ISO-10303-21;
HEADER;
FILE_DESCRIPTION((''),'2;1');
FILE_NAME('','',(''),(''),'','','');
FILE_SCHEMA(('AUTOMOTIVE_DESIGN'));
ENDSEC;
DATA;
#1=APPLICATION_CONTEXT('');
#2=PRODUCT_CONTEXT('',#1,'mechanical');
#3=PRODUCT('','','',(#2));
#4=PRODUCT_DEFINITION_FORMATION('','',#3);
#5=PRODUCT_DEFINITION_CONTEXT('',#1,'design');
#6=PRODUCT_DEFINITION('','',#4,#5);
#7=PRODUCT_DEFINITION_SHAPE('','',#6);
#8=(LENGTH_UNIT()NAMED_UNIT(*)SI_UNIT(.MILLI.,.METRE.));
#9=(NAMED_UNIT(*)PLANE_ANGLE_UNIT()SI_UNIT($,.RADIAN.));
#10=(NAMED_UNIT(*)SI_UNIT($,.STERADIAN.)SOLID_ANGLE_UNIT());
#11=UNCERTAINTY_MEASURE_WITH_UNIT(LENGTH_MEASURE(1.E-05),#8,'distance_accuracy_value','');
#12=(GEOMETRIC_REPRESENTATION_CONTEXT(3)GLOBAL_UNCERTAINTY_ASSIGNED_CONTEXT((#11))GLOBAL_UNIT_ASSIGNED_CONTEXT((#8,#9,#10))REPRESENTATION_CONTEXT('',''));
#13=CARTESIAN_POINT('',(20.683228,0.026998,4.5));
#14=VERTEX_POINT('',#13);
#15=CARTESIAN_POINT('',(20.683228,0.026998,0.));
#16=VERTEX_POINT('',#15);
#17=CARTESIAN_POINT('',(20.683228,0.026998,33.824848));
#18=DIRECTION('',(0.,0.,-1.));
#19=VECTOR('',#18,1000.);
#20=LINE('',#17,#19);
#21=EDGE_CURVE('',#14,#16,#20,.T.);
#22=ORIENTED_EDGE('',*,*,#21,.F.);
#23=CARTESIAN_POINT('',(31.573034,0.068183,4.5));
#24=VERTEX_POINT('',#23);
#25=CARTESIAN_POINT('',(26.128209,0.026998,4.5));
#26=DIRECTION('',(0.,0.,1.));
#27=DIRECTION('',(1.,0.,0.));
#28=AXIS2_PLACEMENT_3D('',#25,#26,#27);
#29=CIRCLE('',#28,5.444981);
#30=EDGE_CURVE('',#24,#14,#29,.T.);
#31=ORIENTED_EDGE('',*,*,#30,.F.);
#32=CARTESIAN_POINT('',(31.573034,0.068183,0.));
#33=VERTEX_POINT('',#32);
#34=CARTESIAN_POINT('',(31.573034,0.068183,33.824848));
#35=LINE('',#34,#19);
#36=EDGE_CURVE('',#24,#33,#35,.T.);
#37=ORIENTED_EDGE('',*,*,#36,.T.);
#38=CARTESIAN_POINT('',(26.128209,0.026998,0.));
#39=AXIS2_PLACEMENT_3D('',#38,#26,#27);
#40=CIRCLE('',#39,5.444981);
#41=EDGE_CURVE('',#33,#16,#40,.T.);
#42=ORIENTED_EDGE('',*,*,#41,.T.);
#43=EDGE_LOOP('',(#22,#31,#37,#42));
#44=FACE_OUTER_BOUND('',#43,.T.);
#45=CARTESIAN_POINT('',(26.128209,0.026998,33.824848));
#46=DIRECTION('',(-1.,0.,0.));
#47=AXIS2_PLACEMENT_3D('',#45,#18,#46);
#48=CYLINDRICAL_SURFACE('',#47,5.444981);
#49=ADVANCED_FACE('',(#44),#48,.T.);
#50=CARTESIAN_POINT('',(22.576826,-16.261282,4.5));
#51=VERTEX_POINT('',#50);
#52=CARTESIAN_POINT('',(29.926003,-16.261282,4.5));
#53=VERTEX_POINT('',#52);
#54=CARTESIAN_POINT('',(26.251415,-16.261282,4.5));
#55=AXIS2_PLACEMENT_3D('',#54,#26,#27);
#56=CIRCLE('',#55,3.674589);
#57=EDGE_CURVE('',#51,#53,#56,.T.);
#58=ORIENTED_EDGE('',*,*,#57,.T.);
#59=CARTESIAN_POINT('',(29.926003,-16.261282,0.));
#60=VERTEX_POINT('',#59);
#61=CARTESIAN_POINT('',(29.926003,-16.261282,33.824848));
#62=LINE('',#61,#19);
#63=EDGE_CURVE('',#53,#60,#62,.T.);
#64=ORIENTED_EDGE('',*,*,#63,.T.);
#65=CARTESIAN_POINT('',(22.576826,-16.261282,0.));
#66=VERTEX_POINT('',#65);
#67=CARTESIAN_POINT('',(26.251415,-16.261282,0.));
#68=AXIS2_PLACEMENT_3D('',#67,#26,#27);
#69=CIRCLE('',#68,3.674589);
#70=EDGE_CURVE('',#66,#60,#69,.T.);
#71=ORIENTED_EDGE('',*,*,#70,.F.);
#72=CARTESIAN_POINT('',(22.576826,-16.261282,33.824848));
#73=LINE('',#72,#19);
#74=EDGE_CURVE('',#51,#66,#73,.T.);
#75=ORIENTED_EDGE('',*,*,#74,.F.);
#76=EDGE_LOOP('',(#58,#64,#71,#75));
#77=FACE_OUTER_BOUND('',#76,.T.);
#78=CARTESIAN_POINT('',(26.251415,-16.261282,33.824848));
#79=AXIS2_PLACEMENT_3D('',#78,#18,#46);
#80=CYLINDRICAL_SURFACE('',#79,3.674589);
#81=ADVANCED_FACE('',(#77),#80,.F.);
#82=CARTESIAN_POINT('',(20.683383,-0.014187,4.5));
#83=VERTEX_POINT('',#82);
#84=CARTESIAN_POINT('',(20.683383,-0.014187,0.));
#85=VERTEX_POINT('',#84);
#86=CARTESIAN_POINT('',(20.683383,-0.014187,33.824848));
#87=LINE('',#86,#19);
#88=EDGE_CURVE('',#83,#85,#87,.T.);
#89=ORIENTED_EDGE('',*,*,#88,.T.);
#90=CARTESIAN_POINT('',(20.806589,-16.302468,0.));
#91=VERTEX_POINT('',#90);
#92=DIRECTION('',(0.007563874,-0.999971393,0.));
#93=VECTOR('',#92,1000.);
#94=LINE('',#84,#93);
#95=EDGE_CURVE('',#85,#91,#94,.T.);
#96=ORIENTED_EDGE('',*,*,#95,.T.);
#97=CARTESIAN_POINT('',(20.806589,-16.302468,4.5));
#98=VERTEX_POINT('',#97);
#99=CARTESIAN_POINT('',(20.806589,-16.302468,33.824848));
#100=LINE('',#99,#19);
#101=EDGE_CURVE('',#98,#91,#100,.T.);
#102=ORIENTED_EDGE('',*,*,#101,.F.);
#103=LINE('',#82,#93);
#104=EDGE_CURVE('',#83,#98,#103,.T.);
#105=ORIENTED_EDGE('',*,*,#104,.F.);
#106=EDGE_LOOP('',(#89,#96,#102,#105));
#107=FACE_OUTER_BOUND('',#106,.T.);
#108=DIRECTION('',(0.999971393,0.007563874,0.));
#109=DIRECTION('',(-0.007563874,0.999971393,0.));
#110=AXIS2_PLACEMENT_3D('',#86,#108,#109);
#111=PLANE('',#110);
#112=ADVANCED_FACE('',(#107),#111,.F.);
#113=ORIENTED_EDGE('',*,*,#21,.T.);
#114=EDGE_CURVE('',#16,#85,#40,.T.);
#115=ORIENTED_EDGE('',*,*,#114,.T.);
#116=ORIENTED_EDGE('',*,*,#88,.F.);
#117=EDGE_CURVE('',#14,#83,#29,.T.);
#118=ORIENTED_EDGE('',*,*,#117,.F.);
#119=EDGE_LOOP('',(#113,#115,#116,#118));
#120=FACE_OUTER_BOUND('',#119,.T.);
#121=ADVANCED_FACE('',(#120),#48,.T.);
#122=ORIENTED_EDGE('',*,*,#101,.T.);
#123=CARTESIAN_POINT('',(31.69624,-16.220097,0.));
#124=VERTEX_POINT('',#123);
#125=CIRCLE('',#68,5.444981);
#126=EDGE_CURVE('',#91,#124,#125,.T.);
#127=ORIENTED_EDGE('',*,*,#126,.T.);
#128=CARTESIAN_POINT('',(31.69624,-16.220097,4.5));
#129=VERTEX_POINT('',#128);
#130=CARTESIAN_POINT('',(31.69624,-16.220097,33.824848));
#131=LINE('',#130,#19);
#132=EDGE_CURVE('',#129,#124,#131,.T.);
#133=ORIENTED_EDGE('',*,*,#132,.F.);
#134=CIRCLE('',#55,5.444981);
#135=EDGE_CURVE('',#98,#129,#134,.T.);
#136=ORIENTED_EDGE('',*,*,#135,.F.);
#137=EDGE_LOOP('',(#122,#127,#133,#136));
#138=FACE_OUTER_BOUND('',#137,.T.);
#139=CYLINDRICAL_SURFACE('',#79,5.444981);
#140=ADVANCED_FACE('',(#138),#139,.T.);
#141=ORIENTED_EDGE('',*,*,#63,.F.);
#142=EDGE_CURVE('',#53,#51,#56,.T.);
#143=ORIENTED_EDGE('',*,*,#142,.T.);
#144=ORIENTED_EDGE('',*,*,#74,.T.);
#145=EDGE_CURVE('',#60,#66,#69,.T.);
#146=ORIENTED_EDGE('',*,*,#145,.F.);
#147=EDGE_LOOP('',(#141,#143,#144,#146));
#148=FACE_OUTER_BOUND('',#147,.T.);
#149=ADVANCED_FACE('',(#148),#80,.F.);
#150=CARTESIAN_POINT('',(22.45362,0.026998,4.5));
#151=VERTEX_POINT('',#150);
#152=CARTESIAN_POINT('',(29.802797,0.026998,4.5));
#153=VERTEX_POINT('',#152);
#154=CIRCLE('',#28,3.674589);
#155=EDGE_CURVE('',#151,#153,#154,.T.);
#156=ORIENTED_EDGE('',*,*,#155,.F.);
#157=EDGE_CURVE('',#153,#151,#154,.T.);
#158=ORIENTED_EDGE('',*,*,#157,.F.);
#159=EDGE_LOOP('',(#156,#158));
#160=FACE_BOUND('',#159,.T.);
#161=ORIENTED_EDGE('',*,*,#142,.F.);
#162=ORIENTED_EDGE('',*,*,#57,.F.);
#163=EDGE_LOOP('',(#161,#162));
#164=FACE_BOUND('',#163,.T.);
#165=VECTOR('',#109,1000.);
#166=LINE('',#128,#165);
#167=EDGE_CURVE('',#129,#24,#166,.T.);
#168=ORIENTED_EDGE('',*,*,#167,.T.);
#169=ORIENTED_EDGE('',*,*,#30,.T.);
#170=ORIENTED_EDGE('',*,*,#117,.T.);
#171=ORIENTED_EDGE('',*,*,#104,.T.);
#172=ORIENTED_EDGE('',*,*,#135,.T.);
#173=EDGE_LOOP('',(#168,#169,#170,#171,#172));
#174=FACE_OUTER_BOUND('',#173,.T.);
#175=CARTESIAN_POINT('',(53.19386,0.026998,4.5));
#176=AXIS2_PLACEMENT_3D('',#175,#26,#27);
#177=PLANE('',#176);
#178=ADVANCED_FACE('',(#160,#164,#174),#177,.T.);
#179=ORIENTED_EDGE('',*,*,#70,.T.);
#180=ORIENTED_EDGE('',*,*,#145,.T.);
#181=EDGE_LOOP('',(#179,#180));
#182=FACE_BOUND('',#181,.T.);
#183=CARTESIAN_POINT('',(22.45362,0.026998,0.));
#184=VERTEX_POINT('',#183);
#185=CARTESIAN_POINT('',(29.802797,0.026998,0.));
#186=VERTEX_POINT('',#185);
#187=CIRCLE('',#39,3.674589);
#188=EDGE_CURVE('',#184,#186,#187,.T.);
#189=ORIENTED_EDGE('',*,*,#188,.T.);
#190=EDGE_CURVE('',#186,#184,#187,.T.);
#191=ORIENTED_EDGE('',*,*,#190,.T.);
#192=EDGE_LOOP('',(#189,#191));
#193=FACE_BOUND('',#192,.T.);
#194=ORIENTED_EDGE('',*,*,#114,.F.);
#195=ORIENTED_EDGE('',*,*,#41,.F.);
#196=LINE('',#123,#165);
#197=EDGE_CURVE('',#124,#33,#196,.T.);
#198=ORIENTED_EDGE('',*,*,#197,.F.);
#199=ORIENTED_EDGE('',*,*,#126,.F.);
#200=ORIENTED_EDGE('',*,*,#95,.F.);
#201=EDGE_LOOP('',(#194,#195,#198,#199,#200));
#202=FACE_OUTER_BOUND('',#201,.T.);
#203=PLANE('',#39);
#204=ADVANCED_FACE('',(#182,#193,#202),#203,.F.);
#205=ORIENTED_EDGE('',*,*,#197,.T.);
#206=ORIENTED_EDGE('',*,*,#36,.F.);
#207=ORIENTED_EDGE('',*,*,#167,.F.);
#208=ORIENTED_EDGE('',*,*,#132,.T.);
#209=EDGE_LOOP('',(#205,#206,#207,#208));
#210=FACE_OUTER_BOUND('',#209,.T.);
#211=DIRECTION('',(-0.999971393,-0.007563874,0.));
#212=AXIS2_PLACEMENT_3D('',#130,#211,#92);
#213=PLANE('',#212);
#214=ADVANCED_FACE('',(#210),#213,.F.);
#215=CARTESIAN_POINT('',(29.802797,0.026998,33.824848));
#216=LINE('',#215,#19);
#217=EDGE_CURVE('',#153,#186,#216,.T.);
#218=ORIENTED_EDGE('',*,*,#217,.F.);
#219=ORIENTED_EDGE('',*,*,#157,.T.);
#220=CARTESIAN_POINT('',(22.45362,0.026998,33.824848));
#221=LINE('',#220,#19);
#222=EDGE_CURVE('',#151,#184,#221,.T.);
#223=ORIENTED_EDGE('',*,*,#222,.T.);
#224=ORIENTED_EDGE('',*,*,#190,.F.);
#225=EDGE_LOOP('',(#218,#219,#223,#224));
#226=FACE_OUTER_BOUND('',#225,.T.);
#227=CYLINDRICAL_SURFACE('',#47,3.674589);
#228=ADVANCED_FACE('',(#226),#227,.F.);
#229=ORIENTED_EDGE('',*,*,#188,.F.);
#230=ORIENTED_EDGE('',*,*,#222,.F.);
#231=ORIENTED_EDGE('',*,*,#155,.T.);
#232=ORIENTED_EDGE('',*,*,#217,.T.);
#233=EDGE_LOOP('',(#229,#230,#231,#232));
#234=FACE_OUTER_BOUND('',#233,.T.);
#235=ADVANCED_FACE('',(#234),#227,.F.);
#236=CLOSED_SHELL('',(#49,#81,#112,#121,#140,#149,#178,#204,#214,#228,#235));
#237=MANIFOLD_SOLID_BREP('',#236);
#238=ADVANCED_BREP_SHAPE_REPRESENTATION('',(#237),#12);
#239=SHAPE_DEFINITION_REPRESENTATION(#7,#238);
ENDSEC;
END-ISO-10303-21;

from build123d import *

# Parameters (mm, degrees)
SKETCH1_R           = 3.674588618
BOSS_EXTRUDE1_DEPTH = 4.5


with BuildPart() as part:
    # Sketch1 → Boss-Extrude1 (new body)
    with BuildSketch(Plane.XY):
        with BuildLine():
            Line((31.69623991, -16.220097286), (31.57303389, 0.068183186))
            ThreePointArc((31.57303389, 0.068183186), (26.087023529, 5.47182325), (20.683383464, -0.014187111))
            Line((20.683383464, -0.014187111), (20.806589485, -16.302467582))
            ThreePointArc((20.806589485, -16.302467582), (26.292599845, -21.706107647), (31.69623991, -16.220097286))
        make_face()
        with Locations((26.128208677, 0.026998038)):
            Circle(SKETCH1_R, mode=Mode.SUBTRACT)
        with Locations((26.251414697, -16.261282434)):
            Circle(SKETCH1_R, mode=Mode.SUBTRACT)
    extrude(amount=BOSS_EXTRUDE1_DEPTH)


solid = part.part
